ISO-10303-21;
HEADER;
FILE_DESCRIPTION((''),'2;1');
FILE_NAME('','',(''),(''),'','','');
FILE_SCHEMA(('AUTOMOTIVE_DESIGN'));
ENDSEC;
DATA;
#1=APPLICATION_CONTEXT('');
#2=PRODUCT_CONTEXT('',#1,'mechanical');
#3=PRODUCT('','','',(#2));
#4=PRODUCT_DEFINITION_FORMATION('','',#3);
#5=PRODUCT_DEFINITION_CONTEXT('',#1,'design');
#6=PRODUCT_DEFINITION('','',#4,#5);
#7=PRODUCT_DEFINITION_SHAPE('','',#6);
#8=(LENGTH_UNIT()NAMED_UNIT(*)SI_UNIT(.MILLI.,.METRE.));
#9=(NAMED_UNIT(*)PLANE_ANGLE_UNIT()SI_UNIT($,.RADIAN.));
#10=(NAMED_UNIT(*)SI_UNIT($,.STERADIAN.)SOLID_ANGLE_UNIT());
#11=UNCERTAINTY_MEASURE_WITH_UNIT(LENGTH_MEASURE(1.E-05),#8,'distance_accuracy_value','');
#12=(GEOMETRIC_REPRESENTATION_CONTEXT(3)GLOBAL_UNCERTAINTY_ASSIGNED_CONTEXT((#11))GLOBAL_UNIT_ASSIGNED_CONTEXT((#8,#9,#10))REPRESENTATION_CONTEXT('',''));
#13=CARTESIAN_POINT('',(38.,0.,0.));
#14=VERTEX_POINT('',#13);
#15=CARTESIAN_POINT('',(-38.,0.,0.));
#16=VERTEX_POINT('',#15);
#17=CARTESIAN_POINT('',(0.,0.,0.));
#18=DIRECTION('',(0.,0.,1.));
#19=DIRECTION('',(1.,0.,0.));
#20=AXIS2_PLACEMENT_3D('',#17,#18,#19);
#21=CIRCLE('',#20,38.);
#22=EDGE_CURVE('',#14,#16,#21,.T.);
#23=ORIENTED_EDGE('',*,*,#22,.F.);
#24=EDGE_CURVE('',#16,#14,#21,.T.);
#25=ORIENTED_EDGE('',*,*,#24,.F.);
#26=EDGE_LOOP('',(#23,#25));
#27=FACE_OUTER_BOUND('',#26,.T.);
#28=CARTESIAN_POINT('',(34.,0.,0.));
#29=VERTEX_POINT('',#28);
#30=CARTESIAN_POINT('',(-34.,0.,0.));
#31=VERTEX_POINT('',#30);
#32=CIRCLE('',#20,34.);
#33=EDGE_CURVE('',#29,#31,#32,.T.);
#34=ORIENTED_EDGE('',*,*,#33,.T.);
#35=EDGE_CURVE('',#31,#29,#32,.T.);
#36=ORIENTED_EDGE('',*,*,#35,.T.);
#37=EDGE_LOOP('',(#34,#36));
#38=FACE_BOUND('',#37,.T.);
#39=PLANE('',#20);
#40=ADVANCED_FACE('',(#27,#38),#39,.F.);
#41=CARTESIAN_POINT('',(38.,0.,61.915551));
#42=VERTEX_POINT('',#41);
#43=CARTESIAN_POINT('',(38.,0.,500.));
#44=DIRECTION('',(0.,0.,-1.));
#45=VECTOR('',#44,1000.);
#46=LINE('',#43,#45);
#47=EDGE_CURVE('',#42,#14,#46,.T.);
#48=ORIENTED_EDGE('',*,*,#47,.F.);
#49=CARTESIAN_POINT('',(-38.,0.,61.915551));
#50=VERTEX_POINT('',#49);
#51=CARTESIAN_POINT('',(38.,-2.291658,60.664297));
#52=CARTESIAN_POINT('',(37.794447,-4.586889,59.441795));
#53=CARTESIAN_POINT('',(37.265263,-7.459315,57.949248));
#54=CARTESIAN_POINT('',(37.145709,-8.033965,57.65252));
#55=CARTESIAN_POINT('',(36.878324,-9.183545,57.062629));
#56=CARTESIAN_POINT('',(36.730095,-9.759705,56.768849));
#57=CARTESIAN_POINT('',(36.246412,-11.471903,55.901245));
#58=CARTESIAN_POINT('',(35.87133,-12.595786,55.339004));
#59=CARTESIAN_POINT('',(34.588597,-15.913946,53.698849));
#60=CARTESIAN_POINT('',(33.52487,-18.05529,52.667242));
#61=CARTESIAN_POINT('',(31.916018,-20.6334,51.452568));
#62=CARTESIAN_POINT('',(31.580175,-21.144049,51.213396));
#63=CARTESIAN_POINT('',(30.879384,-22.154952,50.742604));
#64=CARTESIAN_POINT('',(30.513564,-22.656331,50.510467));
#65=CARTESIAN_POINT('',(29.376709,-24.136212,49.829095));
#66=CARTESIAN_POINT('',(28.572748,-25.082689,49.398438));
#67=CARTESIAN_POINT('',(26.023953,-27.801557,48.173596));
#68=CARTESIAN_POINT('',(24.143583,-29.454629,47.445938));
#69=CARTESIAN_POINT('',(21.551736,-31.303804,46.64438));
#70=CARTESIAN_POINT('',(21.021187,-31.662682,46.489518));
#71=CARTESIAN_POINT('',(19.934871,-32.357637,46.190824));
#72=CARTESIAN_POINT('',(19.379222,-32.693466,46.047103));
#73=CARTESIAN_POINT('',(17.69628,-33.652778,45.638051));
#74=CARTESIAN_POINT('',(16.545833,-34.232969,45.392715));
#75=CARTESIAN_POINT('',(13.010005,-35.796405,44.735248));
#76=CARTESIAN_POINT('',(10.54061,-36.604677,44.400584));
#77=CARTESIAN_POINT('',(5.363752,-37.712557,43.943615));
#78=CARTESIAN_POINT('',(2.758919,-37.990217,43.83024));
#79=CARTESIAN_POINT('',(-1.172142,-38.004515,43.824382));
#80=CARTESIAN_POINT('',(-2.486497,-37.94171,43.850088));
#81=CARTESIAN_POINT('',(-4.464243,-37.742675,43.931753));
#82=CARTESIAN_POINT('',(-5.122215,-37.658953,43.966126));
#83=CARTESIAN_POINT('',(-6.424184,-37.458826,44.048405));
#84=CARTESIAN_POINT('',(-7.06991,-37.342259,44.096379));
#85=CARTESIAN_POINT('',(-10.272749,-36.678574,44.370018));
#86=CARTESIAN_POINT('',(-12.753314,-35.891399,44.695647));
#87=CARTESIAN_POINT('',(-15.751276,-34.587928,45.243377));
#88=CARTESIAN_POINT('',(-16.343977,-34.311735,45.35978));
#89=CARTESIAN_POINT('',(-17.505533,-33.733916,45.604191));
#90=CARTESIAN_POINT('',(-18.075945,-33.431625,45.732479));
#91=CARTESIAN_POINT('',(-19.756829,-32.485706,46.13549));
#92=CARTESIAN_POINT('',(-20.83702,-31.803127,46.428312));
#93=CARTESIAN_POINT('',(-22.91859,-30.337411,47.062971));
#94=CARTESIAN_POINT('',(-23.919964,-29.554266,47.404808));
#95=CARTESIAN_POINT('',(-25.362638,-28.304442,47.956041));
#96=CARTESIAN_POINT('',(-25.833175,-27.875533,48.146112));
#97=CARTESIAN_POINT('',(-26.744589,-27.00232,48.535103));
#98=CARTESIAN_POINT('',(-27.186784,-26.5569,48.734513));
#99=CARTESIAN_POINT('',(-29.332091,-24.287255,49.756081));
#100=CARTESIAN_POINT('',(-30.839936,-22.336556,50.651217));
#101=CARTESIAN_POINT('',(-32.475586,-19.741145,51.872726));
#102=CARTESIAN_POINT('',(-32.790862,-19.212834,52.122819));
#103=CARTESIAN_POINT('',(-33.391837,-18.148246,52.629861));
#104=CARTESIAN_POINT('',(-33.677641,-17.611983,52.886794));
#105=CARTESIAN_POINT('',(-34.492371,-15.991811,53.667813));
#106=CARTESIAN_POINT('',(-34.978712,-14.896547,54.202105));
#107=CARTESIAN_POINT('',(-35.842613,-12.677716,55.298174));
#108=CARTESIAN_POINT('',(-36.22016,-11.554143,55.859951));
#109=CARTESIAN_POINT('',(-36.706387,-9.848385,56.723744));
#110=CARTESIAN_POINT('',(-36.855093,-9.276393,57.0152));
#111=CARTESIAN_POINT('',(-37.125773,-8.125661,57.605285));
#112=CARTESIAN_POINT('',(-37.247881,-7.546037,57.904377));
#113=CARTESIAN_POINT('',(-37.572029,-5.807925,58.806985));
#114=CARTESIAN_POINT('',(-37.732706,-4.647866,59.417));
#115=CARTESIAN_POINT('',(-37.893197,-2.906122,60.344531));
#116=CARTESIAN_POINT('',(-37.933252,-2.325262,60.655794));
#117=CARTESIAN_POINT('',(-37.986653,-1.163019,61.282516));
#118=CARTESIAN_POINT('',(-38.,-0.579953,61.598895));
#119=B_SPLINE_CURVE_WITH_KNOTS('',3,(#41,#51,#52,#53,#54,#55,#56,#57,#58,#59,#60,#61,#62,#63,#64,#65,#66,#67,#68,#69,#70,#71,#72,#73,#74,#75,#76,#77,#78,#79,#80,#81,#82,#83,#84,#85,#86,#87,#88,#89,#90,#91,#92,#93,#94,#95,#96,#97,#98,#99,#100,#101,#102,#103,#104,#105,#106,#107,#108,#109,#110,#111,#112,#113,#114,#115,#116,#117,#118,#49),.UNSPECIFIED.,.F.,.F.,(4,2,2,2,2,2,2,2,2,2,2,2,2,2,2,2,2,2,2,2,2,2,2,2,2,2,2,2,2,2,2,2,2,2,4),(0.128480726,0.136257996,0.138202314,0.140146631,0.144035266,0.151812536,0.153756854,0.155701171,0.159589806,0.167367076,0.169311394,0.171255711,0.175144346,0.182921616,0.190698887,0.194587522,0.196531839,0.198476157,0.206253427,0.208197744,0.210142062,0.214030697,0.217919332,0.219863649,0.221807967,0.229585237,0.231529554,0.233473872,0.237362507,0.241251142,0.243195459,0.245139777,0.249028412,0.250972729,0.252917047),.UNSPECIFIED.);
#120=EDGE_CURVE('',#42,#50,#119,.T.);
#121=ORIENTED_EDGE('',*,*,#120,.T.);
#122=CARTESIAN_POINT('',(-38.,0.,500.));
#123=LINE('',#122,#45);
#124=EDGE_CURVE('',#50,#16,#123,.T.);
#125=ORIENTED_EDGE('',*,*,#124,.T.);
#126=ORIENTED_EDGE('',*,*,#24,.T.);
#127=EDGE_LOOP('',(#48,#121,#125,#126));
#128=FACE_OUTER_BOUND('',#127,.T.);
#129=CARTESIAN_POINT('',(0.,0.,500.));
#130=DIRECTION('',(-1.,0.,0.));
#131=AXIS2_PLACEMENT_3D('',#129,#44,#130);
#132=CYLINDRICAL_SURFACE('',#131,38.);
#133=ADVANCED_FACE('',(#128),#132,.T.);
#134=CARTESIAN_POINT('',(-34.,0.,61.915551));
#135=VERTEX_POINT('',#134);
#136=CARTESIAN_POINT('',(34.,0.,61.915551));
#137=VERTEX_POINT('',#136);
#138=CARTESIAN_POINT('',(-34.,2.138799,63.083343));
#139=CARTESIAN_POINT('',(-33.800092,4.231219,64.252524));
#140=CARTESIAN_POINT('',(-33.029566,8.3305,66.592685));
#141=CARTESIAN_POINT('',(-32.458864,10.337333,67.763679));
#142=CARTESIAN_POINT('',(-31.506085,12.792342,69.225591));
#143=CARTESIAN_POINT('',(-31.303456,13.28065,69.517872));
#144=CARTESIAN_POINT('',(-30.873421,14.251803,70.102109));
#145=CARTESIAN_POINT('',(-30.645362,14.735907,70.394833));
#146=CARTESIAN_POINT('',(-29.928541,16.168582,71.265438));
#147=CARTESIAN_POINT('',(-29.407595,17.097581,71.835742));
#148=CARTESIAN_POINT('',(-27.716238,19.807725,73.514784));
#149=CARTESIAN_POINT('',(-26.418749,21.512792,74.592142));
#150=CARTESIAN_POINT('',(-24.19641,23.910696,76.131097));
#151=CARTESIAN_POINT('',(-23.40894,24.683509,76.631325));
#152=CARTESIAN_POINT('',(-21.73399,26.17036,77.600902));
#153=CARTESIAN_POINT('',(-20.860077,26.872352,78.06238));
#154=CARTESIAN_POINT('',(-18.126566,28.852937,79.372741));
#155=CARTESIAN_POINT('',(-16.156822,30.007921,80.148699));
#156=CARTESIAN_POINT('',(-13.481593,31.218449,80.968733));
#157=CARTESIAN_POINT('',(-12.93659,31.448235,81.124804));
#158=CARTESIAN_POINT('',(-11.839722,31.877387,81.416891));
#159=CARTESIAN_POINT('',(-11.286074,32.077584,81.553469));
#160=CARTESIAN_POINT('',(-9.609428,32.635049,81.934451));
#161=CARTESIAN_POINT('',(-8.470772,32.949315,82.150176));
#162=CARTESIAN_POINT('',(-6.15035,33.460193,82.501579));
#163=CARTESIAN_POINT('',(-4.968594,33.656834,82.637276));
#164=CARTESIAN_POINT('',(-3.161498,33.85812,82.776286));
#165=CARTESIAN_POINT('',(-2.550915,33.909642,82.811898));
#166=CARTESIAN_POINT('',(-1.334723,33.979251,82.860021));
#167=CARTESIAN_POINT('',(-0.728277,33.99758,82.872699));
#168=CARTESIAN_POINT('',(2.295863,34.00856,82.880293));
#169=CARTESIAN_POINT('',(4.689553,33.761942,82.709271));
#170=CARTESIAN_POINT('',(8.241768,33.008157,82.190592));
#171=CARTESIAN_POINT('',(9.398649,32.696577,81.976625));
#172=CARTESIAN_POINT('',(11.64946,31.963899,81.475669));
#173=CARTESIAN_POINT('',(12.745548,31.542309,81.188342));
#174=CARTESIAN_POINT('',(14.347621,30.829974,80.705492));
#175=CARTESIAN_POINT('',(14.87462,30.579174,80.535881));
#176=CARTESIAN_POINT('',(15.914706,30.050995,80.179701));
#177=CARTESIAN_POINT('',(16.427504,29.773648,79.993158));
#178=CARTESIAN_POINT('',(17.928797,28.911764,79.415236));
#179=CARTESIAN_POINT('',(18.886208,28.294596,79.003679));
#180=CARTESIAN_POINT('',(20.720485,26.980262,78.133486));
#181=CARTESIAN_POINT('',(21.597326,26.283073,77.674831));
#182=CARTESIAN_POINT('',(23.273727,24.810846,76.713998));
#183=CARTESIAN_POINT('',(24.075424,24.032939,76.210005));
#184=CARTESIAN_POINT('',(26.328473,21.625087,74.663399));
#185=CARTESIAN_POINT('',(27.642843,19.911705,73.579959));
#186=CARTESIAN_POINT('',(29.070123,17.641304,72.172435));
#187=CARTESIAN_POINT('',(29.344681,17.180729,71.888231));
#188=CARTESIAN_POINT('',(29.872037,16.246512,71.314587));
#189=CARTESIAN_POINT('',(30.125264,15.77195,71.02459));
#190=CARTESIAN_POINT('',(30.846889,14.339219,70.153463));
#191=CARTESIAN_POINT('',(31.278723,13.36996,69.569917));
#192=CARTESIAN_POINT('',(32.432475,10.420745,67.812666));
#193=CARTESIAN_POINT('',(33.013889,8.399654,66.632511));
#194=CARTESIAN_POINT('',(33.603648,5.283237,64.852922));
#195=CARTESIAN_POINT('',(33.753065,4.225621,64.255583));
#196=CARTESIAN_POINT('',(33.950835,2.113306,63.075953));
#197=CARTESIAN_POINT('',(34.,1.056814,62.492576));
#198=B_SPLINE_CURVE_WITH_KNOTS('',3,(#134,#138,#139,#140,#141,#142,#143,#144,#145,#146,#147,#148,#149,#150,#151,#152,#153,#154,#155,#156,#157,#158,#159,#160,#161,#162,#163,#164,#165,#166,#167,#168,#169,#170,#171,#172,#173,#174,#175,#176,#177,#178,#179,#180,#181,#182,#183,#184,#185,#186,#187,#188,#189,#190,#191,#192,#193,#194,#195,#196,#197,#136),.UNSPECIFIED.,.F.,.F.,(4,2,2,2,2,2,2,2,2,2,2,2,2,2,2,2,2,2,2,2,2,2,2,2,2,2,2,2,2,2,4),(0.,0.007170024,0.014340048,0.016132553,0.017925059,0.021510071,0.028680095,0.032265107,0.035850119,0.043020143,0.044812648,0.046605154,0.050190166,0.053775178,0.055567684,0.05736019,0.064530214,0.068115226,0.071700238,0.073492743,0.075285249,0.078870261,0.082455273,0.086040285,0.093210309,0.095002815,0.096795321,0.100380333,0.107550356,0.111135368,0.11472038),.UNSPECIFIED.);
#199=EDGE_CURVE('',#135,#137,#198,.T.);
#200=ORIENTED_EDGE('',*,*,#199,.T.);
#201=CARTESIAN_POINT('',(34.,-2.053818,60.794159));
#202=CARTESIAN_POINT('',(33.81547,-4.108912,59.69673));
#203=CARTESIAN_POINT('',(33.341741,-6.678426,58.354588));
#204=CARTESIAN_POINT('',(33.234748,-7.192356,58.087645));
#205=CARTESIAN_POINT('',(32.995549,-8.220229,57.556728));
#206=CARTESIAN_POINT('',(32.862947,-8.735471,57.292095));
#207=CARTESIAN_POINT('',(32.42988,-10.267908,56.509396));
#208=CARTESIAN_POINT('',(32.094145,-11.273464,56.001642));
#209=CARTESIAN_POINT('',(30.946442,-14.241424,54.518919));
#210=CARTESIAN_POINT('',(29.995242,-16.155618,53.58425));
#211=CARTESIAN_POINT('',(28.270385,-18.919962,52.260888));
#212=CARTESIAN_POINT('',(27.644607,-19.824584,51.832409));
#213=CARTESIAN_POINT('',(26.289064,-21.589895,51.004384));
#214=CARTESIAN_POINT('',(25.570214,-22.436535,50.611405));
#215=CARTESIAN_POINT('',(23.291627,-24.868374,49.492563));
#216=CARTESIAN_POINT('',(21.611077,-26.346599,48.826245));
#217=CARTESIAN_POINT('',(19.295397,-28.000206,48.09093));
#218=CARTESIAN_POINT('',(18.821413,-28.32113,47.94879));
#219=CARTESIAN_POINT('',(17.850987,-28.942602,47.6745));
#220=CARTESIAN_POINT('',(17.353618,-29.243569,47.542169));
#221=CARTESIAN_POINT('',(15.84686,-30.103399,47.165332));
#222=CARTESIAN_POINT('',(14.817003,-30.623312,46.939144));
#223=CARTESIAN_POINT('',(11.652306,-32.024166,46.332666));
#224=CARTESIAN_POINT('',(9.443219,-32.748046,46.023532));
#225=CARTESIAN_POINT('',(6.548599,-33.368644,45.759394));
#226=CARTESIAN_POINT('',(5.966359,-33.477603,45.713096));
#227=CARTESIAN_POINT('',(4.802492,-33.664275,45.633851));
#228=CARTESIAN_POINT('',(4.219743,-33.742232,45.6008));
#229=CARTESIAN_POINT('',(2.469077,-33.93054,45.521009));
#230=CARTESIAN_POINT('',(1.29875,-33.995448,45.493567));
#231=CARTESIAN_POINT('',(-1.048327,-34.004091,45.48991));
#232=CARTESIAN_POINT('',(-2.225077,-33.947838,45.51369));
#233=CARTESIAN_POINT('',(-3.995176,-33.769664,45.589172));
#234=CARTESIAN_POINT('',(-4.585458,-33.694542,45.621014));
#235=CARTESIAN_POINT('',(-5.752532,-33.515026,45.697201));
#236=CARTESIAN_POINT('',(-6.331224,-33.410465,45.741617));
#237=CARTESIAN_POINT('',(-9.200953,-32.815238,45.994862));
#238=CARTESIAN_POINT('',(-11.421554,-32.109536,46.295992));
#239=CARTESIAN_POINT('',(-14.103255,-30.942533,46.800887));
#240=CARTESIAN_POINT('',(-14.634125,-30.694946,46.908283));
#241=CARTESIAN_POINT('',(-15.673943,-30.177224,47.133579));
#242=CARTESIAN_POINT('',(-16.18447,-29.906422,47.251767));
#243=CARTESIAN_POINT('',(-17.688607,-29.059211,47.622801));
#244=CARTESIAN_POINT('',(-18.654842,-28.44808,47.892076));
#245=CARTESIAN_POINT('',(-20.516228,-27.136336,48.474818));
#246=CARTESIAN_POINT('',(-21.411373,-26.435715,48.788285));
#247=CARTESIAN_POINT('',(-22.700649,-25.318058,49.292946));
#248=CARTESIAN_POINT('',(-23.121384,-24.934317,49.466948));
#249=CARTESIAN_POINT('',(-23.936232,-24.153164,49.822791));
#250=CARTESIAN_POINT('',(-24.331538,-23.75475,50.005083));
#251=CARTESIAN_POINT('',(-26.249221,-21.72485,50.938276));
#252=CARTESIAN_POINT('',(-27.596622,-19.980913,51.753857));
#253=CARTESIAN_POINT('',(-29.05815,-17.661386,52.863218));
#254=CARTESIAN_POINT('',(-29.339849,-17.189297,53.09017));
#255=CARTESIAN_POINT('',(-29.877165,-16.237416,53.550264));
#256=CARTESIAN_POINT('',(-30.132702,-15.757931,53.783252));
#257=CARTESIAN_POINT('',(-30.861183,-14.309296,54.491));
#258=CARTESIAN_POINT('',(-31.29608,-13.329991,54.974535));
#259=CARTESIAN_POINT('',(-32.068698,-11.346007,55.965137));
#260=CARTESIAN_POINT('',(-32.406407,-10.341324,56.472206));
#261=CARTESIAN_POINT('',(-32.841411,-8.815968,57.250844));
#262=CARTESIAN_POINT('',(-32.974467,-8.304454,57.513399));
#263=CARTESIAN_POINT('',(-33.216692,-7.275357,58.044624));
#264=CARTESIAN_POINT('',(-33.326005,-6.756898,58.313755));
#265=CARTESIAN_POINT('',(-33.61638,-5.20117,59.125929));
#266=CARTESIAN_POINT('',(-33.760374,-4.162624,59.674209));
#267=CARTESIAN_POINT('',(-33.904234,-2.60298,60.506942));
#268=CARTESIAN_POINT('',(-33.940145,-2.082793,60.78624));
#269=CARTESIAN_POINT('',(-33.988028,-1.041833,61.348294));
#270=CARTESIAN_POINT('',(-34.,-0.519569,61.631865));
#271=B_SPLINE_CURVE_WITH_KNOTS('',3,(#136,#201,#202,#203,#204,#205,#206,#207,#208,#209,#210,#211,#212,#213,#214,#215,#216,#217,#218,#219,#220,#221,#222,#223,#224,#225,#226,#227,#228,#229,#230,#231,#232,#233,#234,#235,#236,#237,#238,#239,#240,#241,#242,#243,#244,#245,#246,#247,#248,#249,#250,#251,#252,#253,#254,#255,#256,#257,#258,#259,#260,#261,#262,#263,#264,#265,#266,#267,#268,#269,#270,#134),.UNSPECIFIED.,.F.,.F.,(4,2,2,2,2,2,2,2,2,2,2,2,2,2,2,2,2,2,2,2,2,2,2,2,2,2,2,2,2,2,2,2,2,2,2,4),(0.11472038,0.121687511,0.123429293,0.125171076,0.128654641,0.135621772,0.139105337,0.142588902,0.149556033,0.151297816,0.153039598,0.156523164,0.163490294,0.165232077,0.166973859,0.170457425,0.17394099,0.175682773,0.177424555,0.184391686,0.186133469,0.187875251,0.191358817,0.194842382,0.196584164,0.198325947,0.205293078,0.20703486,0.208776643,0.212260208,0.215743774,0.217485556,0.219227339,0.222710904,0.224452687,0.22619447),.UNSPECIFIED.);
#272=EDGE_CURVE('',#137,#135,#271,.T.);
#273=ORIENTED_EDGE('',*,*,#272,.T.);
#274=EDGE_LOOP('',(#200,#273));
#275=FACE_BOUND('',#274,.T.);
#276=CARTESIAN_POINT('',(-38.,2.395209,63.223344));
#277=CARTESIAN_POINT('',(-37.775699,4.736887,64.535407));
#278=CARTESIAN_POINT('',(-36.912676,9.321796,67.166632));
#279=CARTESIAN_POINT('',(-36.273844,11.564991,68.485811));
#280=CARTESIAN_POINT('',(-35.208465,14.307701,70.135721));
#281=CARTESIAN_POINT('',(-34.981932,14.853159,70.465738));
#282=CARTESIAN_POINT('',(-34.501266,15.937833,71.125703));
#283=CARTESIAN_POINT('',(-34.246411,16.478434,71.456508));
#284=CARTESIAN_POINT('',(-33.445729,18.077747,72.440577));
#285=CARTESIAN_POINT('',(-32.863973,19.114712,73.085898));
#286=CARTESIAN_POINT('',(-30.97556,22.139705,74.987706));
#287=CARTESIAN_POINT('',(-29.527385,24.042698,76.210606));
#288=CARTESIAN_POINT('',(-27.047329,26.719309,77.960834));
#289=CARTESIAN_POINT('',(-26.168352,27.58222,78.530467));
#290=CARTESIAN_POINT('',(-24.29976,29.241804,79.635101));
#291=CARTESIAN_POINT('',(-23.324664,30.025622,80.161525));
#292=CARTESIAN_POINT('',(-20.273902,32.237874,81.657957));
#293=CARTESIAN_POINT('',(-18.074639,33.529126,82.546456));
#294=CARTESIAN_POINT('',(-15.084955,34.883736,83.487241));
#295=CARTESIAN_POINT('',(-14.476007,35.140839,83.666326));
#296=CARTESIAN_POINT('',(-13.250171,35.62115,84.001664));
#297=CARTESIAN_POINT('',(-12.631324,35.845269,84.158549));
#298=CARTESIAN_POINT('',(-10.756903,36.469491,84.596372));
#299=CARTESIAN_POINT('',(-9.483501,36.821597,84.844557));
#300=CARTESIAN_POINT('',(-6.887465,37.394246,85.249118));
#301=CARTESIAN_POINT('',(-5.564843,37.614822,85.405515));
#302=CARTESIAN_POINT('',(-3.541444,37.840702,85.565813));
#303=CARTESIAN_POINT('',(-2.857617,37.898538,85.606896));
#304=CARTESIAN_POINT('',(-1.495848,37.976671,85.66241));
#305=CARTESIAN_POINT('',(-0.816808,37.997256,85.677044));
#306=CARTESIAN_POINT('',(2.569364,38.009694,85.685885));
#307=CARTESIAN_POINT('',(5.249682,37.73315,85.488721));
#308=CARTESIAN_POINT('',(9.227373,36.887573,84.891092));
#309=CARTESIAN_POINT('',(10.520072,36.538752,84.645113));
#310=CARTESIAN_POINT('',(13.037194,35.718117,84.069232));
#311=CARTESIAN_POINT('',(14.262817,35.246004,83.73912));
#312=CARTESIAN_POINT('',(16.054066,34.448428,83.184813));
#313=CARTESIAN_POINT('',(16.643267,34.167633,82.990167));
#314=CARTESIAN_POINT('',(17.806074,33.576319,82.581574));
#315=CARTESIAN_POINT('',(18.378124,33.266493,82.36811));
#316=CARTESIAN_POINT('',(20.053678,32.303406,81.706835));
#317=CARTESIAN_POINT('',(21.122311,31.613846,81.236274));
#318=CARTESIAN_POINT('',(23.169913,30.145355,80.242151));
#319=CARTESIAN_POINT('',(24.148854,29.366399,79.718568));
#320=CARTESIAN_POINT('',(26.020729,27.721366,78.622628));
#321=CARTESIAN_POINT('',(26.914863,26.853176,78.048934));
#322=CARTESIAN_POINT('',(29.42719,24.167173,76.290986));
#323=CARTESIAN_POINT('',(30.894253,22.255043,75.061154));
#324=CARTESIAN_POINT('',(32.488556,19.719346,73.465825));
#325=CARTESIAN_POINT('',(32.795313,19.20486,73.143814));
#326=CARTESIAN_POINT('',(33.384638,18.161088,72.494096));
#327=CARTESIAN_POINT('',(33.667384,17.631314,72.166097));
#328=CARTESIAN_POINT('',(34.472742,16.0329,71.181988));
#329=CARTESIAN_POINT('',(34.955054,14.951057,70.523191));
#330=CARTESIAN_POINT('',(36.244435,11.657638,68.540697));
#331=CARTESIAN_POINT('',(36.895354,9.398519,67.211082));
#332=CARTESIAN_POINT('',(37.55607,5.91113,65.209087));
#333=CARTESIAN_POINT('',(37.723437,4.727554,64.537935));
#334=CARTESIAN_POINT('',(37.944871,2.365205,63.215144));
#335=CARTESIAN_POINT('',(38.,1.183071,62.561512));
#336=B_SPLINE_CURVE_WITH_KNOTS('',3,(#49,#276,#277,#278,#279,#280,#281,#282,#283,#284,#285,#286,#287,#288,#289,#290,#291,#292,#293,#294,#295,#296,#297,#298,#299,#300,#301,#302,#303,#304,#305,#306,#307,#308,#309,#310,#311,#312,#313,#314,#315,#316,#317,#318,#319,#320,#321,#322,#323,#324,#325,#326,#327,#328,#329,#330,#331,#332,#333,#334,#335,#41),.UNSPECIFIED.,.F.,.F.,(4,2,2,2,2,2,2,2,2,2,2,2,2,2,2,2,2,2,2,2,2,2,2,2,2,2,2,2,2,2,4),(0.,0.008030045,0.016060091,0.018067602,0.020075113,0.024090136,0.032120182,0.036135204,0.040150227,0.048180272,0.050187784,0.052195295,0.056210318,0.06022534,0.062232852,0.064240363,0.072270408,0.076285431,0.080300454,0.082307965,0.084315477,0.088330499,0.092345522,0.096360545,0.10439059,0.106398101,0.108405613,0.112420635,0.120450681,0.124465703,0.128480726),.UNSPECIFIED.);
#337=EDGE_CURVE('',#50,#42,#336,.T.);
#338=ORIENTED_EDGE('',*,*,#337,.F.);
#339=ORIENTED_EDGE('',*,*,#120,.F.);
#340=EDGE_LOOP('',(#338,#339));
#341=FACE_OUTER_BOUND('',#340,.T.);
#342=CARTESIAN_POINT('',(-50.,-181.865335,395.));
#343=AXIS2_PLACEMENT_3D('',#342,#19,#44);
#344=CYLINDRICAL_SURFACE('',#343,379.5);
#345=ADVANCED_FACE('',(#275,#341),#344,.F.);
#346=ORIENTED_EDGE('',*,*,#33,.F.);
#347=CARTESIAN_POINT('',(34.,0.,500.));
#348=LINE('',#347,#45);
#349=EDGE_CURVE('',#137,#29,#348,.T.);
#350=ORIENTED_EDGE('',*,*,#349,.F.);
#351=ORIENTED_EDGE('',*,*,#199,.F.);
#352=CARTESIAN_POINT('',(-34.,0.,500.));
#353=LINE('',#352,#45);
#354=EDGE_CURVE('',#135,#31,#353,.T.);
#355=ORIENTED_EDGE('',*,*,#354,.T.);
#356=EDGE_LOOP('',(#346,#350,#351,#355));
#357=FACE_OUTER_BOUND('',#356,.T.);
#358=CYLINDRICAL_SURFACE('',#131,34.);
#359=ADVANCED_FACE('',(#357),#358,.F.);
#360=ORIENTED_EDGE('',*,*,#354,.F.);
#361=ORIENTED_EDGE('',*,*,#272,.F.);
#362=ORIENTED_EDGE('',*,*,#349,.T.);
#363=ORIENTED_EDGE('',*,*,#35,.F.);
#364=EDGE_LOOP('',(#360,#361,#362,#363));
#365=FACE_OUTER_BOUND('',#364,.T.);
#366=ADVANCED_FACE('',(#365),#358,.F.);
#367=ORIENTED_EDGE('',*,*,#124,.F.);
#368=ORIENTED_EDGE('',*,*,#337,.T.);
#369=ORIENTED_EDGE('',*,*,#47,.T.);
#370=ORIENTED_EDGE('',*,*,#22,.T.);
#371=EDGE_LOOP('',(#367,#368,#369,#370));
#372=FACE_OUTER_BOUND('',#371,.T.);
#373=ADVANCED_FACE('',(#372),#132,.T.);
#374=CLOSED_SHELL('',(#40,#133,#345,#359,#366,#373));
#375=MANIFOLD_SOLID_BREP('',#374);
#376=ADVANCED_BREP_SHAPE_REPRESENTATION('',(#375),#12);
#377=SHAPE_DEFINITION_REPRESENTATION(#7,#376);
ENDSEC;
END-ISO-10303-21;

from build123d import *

# Parameters (mm, degrees)
SKETCH1_R           = 38
SKETCH1_R_2         = 34
BOSS_EXTRUDE1_DEPTH = 500
SKETCH2_R           = 379.5
CUT_EXTRUDE1_DEPTH  = 50


with BuildPart() as part:
    # Sketch1 → Boss-Extrude1 (new body)
    with BuildSketch(Plane.XY):
        Circle(SKETCH1_R)
        Circle(SKETCH1_R_2, mode=Mode.SUBTRACT)
    extrude(amount=BOSS_EXTRUDE1_DEPTH)

    # Sketch2 → Cut-Extrude1 (cut, symmetric)
    with BuildSketch(Plane(origin=(0, 0, 0), x_dir=(0, 0, -1), z_dir=(1, 0, 0))):
        with Locations((-395, -181.865334795)):
            Circle(SKETCH2_R)
    extrude(amount=CUT_EXTRUDE1_DEPTH, both=True, mode=Mode.SUBTRACT)


solid = part.part
